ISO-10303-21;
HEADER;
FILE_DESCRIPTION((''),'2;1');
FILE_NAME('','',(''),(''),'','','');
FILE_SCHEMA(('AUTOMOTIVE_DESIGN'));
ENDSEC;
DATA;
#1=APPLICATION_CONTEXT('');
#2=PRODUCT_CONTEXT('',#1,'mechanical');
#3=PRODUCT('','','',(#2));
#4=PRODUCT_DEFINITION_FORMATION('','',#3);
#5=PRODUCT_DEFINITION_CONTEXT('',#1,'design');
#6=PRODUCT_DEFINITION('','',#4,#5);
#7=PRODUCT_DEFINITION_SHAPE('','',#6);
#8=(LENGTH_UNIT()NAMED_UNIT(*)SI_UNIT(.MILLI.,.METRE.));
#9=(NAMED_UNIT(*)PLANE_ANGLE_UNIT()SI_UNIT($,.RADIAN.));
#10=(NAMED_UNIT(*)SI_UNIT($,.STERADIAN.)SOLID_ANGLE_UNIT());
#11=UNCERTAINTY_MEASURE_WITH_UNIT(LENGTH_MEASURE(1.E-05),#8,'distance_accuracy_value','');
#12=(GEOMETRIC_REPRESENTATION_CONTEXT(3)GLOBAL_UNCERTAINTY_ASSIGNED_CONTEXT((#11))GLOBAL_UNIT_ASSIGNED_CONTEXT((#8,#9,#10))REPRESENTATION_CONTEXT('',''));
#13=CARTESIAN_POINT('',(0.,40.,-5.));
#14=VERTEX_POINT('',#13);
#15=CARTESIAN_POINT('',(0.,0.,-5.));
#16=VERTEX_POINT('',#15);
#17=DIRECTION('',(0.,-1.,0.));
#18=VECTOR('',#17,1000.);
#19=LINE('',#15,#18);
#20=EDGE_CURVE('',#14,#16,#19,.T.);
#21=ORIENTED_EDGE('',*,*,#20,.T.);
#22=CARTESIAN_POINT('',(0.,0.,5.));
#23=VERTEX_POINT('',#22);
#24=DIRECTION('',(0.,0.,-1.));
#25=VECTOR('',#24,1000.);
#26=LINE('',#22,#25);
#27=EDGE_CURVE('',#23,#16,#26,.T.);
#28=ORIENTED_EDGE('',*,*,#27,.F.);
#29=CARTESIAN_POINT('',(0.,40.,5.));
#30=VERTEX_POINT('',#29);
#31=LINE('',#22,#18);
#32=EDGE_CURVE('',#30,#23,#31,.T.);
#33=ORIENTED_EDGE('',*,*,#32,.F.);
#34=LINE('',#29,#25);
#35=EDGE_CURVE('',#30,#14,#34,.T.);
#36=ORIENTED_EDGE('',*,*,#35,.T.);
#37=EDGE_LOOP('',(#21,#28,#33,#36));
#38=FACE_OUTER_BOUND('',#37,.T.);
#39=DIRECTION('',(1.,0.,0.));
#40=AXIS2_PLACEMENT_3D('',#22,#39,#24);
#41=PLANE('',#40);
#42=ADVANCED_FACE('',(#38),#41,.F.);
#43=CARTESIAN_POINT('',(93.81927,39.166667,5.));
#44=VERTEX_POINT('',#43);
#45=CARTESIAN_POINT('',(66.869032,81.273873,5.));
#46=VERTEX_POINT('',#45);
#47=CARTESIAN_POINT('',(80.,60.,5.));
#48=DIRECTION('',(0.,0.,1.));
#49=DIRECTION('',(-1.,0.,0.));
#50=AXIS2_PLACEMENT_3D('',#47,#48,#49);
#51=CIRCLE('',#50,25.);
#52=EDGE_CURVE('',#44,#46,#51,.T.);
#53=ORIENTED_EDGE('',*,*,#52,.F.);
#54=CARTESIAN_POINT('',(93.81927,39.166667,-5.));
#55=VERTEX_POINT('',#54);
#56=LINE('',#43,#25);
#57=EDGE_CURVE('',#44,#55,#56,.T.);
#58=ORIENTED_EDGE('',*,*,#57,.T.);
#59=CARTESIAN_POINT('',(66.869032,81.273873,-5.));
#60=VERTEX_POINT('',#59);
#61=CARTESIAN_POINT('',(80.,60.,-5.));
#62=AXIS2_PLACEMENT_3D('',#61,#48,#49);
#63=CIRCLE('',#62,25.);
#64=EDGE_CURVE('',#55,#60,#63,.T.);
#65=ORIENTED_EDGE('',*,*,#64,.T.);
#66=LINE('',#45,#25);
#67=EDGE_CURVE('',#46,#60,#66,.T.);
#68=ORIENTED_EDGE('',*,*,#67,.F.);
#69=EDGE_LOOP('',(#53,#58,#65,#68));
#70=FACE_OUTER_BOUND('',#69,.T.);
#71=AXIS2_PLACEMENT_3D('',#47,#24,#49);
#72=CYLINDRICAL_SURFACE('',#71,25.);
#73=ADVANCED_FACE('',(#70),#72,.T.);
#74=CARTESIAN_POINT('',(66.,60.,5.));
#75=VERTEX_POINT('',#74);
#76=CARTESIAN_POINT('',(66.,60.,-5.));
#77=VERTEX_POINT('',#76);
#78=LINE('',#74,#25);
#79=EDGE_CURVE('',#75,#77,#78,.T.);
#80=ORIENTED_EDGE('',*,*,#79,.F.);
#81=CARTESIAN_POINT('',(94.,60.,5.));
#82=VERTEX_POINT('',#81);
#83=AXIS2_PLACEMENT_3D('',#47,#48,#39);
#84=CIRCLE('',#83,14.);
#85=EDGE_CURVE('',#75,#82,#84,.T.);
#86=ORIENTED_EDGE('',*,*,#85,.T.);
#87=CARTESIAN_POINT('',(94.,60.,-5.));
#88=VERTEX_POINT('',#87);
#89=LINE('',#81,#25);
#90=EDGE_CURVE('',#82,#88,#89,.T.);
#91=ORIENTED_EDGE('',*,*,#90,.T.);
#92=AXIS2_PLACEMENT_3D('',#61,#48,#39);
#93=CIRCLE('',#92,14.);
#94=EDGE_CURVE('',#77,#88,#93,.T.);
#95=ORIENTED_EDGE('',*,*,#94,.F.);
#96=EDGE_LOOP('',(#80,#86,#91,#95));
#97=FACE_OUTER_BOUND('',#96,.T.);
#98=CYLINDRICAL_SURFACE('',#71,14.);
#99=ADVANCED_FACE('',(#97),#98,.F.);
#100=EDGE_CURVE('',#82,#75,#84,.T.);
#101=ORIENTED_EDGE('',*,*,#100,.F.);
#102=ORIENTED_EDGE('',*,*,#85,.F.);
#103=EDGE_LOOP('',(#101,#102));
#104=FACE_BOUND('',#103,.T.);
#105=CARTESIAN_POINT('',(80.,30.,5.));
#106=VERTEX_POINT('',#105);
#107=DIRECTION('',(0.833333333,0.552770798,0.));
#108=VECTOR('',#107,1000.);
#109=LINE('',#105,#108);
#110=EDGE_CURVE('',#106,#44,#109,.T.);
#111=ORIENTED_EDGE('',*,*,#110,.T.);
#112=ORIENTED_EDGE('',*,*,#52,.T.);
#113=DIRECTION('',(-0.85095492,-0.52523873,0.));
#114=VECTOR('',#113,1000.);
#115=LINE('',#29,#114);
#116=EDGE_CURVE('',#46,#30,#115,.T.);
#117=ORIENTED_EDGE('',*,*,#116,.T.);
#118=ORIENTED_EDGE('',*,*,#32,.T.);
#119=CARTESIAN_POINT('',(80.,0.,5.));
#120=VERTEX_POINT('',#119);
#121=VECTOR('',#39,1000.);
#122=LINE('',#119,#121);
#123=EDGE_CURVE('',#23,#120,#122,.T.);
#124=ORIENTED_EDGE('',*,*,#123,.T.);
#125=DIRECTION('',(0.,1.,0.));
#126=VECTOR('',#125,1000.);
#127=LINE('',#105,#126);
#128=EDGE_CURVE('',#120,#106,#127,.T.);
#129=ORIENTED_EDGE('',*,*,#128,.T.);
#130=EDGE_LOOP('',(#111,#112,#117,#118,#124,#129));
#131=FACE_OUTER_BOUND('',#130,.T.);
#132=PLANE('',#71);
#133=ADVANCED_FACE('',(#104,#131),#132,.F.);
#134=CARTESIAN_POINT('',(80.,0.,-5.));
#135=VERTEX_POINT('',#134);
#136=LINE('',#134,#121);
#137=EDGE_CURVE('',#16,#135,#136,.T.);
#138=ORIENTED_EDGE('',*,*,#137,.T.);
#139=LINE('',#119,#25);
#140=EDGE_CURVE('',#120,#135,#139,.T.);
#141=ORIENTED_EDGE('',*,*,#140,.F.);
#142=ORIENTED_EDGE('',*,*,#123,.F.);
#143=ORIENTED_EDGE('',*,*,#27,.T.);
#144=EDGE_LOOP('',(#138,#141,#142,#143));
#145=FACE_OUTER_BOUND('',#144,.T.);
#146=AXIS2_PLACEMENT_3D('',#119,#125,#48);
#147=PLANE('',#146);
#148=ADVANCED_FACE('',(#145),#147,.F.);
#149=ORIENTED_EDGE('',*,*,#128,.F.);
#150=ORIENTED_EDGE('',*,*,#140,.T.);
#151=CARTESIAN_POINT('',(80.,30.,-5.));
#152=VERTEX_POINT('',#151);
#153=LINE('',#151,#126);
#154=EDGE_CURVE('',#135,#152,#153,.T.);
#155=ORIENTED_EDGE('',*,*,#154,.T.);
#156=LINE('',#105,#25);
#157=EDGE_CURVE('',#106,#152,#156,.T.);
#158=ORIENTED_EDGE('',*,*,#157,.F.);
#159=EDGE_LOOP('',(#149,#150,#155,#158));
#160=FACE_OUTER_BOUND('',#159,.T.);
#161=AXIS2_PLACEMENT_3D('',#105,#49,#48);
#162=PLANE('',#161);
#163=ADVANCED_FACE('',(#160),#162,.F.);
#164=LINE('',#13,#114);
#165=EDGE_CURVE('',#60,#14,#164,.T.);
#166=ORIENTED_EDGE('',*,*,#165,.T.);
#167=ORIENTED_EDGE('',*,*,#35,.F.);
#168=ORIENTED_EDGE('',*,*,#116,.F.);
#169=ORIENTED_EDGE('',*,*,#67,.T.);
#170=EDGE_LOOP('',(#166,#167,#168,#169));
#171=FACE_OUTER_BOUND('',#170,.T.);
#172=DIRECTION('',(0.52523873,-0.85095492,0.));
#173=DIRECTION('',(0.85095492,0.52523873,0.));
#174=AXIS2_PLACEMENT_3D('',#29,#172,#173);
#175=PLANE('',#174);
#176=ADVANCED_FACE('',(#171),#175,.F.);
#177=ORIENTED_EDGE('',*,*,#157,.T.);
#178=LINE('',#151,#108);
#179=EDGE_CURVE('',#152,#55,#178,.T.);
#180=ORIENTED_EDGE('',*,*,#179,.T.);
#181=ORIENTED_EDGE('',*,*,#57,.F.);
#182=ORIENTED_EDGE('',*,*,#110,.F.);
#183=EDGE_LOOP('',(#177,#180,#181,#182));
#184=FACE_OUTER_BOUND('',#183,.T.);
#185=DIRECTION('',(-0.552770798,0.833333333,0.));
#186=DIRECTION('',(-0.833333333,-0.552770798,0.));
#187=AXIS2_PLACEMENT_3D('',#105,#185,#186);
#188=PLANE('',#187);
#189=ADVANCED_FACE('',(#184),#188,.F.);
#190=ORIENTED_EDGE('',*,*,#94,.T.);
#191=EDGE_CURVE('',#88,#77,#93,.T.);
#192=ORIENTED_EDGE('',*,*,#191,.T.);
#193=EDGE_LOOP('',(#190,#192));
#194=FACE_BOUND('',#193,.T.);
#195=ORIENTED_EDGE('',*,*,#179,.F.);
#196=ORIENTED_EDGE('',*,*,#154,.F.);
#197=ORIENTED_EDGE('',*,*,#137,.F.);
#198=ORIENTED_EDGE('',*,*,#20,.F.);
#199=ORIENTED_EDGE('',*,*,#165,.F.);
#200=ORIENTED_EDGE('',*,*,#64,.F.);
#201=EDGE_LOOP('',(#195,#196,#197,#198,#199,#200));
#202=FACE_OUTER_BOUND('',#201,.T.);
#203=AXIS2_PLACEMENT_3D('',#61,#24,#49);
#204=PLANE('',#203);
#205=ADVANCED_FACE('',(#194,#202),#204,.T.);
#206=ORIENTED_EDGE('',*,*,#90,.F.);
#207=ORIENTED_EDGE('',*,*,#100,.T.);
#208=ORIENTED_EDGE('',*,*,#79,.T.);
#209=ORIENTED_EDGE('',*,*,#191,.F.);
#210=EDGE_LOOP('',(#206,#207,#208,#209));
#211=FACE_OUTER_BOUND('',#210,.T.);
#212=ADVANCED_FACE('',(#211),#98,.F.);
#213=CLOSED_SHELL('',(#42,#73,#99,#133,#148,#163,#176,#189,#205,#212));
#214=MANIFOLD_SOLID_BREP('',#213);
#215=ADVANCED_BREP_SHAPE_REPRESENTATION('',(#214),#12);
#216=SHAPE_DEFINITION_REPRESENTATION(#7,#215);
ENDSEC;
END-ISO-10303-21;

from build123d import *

# Parameters (mm, degrees)
SKETCH1_R           = 14
BOSS_EXTRUDE1_DEPTH = 5


with BuildPart() as part:
    # Sketch1 → Boss-Extrude1 (new, symmetric)
    with BuildSketch(Plane.XY):
        with BuildLine():
            Line((0, 0), (0, 40))
            Line((0, 40), (66.869031748, 81.273873008))
            ThreePointArc((66.869031748, 81.273873008), (101.056415799, 73.476919296), (93.81926996, 39.166666667))
            Line((93.81926996, 39.166666667), (80, 30))
            Line((80, 30), (80, 0))
            Line((80, 0), (0, 0))
        make_face()
        with Locations((80, 60)):
            Circle(SKETCH1_R, mode=Mode.SUBTRACT)
    extrude(amount=BOSS_EXTRUDE1_DEPTH, both=True)


solid = part.part
